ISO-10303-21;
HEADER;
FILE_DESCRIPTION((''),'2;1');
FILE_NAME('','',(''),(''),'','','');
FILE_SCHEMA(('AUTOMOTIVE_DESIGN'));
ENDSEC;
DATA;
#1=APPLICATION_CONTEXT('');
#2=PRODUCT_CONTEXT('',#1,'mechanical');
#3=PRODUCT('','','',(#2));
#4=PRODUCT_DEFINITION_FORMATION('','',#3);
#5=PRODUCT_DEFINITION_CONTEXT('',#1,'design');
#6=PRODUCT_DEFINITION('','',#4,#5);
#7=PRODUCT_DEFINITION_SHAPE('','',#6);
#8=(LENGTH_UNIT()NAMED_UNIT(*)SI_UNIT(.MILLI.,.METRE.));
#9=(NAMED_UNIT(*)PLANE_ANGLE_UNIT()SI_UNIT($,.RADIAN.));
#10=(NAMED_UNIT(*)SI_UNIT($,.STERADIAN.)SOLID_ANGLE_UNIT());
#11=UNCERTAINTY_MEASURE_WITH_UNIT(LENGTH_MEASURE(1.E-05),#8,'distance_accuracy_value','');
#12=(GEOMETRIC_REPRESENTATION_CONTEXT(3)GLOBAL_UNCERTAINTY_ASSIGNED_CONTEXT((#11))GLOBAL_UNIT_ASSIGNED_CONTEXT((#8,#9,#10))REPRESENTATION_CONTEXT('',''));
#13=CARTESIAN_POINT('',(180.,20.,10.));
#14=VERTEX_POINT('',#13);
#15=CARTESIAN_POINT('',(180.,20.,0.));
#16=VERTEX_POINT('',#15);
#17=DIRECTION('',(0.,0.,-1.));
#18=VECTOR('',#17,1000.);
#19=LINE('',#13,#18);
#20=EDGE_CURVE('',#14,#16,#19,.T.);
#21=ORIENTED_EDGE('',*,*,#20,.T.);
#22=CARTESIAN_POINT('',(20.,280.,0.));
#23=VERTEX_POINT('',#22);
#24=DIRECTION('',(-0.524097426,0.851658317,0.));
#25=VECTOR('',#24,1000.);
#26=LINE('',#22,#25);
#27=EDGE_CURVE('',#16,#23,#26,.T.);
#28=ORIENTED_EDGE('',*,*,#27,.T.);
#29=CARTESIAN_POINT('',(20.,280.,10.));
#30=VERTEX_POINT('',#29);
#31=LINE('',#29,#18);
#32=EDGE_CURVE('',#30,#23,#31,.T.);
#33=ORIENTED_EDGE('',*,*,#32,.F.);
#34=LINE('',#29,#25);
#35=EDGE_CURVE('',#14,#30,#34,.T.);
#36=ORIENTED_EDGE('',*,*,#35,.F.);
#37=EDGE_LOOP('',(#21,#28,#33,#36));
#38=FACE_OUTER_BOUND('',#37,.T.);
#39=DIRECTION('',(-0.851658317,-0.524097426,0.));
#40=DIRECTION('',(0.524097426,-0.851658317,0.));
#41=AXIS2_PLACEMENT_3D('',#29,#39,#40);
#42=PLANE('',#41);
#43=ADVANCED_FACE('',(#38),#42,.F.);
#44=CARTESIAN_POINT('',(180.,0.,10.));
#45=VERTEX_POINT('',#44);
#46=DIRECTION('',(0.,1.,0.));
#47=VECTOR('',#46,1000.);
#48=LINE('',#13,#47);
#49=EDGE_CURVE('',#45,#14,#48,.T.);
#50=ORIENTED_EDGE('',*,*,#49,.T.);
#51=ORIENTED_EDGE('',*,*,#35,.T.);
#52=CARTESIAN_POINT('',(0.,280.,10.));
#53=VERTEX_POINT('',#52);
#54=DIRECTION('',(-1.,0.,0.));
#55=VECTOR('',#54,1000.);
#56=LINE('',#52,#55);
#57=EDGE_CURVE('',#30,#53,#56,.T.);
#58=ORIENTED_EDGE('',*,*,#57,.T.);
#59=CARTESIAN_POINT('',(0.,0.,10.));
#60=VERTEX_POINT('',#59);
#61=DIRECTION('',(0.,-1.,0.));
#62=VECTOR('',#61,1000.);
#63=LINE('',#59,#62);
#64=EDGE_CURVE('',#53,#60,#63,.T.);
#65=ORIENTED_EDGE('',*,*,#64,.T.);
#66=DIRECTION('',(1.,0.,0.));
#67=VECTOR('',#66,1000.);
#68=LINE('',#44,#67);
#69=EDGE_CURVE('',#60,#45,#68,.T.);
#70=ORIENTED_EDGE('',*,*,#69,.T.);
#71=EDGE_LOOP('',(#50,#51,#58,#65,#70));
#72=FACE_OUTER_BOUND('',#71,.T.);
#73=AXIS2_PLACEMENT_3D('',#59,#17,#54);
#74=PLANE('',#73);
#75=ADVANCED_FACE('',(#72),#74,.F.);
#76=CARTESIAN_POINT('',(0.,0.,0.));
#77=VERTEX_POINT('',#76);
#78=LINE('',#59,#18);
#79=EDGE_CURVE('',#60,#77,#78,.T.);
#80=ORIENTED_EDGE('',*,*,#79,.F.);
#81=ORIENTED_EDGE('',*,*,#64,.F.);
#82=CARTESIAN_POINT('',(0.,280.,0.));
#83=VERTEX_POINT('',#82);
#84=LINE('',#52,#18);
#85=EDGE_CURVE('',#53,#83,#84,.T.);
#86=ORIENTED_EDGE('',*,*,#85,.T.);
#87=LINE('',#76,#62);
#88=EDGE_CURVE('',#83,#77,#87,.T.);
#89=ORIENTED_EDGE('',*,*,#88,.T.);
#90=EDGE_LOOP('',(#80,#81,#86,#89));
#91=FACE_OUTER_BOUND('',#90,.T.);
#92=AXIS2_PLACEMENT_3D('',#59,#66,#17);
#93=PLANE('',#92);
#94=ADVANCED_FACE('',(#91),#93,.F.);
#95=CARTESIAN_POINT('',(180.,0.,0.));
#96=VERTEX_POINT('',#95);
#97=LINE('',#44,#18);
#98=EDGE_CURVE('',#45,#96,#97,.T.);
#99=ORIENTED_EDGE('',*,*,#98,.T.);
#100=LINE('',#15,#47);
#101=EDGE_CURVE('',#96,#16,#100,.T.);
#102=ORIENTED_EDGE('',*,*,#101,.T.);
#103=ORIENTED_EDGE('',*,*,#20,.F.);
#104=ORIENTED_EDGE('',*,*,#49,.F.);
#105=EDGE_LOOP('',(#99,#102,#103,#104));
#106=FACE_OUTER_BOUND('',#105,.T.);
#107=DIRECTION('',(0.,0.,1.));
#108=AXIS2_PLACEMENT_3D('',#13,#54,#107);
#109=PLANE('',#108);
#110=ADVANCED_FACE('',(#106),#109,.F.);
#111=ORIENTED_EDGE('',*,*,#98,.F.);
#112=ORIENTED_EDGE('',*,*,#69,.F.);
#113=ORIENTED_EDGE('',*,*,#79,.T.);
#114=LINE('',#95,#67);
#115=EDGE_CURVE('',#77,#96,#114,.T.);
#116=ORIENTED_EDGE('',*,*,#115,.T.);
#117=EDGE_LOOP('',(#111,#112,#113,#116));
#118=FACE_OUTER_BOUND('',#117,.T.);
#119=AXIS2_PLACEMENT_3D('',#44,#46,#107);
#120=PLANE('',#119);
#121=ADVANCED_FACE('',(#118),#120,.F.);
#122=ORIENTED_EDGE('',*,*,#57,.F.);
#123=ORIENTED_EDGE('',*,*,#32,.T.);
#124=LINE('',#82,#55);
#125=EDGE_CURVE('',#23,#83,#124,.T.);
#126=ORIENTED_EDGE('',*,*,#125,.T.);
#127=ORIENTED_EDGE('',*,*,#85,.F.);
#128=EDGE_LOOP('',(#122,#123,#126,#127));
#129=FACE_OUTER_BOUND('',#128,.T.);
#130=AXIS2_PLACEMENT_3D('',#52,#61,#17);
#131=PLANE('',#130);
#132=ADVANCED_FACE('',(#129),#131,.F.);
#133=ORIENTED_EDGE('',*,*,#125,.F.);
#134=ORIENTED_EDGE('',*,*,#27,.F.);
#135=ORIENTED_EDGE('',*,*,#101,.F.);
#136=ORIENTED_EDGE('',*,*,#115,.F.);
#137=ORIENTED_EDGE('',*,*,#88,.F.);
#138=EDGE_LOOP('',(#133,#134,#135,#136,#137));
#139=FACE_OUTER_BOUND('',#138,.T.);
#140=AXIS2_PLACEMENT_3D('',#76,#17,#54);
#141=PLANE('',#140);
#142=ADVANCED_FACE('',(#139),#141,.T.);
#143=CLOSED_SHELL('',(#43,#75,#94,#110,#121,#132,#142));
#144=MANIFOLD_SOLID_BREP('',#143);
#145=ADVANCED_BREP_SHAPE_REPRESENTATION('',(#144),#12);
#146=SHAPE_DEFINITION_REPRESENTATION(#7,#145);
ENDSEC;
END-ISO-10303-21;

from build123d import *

# Parameters (mm, degrees)
BOSS_EXTRUDE1_DEPTH = 10


with BuildPart() as part:
    # Sketch1 → Boss-Extrude1 (new body)
    with BuildSketch(Plane.XY):
        Polygon((0, 0), (0, 280), (20, 280), (180, 20), (180, 0), align=None)
    extrude(amount=BOSS_EXTRUDE1_DEPTH)


solid = part.part
